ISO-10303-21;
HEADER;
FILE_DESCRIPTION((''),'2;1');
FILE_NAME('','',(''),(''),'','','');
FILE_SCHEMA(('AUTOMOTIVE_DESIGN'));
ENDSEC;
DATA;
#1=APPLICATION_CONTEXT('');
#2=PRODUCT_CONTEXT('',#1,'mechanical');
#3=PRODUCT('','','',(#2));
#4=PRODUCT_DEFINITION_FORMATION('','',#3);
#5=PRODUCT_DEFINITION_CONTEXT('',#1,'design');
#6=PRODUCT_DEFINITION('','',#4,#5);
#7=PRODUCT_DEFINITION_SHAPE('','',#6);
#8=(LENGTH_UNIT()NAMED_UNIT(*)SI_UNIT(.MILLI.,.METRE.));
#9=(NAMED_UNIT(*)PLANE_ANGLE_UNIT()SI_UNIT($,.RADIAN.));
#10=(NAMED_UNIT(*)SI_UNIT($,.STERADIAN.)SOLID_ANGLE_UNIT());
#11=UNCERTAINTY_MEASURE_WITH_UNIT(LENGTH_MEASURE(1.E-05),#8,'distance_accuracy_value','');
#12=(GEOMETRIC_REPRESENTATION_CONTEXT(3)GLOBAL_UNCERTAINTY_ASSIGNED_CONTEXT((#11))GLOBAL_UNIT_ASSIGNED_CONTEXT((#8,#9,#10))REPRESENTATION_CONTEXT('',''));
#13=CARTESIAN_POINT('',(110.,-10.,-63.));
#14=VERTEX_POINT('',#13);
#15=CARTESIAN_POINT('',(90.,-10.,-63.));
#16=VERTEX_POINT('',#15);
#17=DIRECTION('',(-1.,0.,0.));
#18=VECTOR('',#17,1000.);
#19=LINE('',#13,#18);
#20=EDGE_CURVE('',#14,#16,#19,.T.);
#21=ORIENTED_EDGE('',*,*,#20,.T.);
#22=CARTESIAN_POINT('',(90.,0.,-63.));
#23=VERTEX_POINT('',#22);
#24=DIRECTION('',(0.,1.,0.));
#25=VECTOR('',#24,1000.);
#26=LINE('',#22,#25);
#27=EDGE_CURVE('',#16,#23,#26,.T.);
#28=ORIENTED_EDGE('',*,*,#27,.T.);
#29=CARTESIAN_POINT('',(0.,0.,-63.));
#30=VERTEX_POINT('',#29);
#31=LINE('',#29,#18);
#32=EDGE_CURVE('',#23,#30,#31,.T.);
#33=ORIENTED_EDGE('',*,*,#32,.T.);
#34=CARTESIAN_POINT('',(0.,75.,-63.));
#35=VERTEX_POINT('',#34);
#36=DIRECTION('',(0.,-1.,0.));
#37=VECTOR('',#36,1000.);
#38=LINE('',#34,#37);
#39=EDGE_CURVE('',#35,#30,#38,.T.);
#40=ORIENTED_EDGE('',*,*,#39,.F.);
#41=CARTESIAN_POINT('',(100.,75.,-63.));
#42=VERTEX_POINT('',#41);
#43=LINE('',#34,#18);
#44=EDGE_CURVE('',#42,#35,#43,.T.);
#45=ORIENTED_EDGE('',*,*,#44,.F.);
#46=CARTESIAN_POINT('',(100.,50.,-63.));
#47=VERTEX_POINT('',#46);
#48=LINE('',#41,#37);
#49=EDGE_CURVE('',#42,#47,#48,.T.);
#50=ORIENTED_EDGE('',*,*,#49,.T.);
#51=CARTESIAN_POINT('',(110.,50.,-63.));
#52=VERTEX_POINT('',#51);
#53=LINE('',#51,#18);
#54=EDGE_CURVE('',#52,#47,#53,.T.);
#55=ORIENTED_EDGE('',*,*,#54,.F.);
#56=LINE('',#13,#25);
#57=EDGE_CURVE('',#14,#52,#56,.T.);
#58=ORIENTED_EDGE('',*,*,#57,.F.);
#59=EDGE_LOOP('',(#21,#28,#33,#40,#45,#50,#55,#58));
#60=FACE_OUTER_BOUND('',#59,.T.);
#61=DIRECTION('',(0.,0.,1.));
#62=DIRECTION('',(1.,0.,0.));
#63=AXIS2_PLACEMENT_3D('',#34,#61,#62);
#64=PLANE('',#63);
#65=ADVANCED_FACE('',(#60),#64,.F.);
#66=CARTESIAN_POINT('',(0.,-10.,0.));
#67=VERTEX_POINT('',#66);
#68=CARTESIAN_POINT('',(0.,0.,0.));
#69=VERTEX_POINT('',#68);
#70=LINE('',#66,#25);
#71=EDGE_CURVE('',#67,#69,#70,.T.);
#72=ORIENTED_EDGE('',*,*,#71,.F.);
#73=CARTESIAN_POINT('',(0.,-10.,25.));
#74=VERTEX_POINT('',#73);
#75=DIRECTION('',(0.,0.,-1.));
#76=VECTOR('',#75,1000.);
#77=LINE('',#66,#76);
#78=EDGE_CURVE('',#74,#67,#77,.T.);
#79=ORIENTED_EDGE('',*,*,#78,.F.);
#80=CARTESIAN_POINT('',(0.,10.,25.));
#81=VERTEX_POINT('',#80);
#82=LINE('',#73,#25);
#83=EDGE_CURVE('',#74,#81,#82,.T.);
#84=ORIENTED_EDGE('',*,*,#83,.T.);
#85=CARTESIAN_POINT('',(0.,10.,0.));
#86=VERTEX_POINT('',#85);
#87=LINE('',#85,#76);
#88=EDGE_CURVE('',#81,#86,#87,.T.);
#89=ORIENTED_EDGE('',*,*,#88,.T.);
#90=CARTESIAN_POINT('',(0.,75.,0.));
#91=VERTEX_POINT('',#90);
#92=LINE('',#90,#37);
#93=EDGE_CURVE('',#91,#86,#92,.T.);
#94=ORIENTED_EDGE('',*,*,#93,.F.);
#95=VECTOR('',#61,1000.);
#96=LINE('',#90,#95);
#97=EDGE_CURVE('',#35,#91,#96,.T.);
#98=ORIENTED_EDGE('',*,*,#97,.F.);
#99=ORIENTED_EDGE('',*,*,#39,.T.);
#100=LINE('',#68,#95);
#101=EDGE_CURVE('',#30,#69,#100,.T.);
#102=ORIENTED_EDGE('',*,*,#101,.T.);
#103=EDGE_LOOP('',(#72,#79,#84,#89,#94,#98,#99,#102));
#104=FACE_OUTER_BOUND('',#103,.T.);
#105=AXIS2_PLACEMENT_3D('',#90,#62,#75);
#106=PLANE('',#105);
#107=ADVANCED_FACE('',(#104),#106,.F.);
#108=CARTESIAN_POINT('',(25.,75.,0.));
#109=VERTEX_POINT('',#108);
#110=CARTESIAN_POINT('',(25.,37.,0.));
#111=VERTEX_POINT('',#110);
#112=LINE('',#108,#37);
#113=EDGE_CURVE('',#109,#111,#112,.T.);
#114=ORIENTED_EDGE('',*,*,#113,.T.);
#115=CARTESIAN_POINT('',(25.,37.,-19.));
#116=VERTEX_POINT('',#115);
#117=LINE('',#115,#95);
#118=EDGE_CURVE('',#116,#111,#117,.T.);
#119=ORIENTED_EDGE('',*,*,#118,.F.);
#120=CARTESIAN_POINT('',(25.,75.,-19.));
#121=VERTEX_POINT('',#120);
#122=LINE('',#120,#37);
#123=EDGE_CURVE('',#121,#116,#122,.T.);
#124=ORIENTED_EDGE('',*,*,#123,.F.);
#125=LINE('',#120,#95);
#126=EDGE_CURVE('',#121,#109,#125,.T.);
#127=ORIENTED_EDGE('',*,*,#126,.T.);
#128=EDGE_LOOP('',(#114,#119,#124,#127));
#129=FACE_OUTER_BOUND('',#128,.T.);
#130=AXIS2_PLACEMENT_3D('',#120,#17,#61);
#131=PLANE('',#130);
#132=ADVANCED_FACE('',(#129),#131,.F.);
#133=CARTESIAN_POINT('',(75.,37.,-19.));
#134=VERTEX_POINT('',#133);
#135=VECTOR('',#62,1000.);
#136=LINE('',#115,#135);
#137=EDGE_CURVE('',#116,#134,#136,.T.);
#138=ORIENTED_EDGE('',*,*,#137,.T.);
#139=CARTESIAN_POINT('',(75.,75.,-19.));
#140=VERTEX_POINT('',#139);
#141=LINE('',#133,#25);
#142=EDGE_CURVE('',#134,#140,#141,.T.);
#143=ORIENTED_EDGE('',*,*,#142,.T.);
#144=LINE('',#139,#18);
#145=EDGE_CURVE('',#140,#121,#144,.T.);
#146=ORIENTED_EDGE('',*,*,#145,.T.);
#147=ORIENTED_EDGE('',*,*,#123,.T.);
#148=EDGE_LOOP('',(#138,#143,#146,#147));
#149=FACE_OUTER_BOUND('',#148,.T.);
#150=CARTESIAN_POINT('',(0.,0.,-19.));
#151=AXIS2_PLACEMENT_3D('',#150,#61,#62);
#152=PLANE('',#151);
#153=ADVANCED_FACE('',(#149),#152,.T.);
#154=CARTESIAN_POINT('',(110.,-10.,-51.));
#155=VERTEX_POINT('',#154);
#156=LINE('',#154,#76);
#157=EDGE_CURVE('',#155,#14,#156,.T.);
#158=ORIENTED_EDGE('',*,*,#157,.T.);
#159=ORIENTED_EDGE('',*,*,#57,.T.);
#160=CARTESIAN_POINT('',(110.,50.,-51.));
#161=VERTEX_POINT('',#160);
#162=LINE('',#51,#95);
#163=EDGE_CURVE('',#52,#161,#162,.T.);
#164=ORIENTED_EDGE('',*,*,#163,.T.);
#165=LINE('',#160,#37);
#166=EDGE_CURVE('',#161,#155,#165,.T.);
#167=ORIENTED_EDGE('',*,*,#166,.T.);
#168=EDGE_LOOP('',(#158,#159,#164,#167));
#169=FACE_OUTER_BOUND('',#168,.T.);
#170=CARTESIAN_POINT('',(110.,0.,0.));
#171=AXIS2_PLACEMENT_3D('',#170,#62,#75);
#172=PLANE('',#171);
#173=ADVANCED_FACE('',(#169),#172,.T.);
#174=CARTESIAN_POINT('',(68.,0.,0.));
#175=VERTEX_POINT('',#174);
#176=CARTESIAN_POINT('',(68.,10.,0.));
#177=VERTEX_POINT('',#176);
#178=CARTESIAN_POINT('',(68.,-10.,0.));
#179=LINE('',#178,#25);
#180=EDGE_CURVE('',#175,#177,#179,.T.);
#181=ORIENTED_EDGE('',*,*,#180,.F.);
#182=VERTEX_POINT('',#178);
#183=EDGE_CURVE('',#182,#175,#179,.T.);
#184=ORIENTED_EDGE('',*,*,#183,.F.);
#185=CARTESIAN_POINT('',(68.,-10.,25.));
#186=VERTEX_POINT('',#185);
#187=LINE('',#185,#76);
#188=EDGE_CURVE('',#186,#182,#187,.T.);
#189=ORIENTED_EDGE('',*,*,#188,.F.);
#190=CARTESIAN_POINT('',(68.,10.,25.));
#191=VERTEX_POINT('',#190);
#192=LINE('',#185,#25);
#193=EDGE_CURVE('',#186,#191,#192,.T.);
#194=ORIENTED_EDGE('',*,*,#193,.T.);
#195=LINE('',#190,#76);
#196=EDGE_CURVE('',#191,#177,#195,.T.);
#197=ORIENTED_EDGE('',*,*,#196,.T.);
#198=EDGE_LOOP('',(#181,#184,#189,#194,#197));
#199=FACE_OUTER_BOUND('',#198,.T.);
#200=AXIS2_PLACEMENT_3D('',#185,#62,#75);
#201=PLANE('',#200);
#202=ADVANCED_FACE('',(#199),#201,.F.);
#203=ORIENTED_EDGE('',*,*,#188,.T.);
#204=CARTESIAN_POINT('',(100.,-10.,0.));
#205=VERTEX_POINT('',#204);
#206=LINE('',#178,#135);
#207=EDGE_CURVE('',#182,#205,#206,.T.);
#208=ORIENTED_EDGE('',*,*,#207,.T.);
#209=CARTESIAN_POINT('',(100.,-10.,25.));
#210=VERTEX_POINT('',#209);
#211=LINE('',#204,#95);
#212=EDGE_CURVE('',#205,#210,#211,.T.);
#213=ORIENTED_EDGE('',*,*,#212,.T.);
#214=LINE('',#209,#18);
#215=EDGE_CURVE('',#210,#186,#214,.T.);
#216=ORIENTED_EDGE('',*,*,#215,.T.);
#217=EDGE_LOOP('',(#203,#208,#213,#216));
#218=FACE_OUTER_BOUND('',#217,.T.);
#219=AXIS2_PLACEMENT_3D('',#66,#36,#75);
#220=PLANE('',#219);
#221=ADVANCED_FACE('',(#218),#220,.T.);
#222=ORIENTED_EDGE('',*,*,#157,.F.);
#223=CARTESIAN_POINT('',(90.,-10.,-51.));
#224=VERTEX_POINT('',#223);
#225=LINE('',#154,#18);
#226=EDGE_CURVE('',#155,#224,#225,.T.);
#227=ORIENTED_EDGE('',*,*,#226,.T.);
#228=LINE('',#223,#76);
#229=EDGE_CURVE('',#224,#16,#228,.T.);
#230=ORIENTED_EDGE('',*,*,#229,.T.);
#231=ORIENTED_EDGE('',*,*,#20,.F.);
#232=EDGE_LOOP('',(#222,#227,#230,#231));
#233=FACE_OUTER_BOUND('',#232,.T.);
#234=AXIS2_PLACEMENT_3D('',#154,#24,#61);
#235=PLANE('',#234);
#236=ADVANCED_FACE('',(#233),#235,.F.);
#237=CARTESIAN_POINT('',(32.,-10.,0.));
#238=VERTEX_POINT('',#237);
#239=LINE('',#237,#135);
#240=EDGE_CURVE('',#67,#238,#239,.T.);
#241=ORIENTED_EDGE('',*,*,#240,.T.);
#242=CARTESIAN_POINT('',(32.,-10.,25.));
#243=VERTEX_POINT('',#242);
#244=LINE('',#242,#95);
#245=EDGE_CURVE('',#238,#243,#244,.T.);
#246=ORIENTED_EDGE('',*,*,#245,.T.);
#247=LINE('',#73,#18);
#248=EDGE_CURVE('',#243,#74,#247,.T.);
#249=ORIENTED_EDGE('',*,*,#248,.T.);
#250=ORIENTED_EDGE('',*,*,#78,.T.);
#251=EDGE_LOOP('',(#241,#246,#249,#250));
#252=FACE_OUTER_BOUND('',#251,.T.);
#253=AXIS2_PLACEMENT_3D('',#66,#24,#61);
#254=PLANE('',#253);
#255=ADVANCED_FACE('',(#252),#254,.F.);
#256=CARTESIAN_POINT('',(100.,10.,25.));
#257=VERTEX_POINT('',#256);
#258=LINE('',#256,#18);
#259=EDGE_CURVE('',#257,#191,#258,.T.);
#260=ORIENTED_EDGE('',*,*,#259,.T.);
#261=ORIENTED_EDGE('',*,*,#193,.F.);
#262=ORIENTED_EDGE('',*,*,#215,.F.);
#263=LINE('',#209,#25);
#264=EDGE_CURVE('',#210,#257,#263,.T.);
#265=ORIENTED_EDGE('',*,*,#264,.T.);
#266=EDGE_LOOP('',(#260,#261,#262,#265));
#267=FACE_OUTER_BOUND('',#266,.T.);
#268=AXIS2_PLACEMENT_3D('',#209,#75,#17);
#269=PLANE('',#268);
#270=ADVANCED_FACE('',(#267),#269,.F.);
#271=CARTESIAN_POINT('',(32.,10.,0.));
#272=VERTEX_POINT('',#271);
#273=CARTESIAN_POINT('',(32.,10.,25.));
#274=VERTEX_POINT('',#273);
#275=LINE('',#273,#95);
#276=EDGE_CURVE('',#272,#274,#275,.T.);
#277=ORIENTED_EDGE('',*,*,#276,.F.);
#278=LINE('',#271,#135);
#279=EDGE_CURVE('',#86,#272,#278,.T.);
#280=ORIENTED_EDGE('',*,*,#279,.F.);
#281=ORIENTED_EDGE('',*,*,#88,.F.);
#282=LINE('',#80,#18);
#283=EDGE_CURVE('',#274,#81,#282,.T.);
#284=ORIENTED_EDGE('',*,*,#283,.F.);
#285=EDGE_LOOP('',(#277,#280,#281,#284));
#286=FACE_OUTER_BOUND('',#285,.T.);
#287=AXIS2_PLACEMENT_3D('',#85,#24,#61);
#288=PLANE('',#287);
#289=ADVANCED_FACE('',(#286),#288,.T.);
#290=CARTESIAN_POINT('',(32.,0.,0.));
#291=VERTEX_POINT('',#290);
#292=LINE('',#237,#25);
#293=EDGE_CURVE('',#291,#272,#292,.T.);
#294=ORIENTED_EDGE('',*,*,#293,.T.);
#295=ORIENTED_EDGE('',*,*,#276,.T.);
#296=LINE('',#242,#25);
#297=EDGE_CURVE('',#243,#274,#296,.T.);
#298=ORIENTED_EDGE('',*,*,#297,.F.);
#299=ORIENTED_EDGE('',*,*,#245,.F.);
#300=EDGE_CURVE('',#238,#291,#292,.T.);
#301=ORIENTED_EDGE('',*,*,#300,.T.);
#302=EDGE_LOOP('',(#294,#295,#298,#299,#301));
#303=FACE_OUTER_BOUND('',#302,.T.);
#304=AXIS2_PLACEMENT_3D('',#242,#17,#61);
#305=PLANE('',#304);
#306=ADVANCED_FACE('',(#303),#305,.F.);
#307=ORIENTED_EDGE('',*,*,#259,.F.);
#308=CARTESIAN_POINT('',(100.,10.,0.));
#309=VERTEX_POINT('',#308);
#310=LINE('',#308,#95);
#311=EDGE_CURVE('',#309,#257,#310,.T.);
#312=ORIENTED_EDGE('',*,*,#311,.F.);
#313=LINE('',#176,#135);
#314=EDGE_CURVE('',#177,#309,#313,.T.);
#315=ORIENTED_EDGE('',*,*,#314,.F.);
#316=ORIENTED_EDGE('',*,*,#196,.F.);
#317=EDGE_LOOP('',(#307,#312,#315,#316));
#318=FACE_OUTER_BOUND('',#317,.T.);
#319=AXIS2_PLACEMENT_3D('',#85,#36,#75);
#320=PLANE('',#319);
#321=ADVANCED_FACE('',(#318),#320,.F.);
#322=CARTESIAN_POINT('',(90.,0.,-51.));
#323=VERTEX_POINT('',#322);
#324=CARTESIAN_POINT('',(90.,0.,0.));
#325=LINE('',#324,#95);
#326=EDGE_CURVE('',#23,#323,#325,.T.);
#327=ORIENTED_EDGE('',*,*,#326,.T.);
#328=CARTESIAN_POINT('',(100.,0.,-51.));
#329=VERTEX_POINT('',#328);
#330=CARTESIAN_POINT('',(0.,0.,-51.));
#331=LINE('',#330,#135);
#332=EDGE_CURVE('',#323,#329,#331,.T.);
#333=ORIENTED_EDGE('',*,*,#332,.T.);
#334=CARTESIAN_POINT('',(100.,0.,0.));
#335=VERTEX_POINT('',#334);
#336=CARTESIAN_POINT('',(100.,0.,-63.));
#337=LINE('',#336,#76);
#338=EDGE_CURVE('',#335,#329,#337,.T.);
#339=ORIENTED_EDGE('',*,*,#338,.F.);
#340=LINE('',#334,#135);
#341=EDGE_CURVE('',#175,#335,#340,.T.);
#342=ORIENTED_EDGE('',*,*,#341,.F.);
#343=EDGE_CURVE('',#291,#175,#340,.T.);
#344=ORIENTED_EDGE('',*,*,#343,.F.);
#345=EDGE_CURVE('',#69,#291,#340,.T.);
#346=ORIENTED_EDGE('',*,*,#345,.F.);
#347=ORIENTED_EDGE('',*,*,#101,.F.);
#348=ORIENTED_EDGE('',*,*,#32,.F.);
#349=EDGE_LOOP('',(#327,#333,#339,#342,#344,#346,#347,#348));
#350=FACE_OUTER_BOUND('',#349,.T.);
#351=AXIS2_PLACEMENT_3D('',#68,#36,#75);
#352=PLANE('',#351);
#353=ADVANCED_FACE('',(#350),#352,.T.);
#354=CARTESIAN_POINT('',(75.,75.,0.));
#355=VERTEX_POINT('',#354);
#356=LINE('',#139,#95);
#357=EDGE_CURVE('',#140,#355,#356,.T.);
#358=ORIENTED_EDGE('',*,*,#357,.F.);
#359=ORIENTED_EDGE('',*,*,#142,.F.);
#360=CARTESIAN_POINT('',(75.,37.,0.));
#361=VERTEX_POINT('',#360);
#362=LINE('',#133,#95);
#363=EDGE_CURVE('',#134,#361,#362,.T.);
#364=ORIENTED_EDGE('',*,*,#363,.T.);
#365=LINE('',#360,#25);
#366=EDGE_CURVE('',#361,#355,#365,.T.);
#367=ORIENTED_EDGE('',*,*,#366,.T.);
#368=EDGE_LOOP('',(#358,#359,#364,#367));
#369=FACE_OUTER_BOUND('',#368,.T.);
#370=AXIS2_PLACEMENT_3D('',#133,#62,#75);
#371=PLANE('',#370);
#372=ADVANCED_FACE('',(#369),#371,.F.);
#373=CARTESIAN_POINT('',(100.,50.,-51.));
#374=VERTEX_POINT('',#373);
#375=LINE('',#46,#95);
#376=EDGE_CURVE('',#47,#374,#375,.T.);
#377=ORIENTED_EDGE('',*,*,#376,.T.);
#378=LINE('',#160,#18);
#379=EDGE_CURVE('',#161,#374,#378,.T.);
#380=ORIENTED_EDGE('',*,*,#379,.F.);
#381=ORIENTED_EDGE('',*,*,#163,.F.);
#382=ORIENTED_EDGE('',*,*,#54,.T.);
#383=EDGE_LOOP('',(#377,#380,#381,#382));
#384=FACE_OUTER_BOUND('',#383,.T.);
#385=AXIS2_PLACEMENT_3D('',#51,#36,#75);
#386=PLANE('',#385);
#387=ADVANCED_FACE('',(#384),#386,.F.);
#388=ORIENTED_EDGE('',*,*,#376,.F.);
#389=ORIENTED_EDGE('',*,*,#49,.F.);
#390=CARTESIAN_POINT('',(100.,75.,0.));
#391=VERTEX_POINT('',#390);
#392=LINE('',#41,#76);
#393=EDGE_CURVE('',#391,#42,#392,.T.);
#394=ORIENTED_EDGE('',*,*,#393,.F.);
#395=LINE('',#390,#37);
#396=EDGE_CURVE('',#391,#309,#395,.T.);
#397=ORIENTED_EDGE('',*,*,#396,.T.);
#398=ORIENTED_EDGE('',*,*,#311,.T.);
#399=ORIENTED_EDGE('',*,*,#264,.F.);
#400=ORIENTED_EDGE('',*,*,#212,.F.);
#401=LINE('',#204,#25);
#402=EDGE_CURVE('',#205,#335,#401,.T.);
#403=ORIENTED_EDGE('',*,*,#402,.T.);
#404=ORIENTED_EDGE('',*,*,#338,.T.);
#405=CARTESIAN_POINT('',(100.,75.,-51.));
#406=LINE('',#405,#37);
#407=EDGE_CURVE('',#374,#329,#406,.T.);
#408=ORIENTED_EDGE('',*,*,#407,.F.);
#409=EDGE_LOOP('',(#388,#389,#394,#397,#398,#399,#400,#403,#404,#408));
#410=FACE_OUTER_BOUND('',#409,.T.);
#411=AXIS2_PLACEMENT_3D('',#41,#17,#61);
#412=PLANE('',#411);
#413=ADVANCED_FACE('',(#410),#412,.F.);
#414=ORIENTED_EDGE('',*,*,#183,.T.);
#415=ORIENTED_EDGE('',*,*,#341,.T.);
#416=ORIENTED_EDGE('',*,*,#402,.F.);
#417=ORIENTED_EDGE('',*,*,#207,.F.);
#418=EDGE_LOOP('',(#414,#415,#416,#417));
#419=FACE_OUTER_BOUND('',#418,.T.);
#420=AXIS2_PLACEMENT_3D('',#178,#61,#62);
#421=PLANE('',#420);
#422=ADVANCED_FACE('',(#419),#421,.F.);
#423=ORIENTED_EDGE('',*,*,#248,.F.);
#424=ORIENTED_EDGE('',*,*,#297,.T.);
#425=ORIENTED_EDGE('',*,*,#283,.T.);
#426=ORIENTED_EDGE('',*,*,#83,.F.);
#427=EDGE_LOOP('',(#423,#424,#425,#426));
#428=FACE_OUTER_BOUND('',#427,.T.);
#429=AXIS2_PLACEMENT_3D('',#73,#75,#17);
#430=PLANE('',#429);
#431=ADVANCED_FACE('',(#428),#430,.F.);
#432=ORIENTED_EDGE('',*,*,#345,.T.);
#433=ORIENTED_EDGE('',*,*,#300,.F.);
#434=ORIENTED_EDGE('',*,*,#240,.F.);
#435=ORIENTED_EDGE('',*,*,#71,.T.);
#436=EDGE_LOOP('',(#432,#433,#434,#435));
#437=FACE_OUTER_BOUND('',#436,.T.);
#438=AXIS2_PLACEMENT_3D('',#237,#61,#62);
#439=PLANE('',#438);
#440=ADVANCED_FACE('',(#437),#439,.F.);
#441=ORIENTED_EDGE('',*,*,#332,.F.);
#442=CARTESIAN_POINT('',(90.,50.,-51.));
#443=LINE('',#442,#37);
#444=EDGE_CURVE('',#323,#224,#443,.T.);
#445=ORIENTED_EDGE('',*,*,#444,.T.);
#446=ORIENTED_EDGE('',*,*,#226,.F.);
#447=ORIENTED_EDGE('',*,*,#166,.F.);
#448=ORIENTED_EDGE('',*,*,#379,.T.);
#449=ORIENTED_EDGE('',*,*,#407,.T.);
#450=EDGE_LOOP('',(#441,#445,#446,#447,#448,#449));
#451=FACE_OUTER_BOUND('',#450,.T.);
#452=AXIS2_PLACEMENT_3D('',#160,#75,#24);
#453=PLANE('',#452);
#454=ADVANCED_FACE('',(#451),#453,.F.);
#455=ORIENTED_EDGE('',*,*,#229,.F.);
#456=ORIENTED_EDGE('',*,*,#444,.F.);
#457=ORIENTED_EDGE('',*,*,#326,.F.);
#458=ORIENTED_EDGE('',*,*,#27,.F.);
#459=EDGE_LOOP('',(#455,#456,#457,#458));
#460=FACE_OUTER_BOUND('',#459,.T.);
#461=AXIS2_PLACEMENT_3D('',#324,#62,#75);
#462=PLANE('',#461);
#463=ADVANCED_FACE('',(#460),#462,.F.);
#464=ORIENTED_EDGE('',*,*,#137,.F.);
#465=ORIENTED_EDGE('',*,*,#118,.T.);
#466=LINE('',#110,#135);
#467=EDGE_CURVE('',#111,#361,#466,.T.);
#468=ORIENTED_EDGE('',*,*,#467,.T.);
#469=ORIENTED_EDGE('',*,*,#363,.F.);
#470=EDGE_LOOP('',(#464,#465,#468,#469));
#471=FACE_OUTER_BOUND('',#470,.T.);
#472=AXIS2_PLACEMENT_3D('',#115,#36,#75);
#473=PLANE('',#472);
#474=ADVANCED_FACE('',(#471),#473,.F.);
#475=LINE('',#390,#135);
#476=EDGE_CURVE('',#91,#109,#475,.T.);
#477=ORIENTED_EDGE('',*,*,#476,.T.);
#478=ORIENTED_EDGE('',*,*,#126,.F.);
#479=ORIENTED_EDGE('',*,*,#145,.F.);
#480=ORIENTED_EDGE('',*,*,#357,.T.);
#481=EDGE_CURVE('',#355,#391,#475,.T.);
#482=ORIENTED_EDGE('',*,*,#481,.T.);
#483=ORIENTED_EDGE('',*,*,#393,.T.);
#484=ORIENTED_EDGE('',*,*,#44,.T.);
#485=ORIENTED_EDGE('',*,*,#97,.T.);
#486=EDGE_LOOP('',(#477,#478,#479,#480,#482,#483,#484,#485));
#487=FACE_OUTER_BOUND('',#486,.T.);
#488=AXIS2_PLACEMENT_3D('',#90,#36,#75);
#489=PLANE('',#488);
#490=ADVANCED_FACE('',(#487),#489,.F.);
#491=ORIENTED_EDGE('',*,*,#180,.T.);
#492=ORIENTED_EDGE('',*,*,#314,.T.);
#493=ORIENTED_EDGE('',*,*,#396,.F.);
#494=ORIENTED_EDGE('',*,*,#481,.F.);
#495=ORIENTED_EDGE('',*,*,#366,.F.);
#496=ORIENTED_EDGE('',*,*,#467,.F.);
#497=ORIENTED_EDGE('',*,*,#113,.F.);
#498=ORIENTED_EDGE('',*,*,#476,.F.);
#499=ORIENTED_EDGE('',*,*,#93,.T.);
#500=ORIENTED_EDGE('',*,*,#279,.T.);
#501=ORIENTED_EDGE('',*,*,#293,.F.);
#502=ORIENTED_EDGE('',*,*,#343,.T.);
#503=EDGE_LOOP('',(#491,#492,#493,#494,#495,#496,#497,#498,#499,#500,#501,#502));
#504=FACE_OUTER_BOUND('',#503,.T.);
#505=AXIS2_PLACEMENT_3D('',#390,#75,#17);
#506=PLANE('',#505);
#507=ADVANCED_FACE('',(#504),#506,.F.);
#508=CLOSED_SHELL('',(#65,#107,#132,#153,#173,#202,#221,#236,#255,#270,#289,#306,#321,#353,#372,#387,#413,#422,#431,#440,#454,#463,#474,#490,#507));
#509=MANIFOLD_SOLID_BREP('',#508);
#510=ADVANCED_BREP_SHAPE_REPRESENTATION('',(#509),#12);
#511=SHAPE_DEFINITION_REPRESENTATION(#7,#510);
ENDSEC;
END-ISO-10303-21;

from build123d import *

# Parameters (mm, degrees)
BASE_BLOCK_SKETCH_W        = 100
BASE_BLOCK_SKETCH_H        = 63
BASE_BLOCK_100X63X75_DEPTH = 75
TOP_POCKET_SKETCH_W        = 50
TOP_POCKET_SKETCH_H        = 38
TOP_POCKET_38X25X19_DEPTH  = 19
FEET_SKETCH_W              = 32
FEET_SKETCH_H              = 25
FEET_2X_32X25_DEPTH        = 10
SIDE_RIB_DEPTH             = 10


with BuildPart() as part:
    # Base Block Sketch → Base Block 100x63x75 (new body)
    with BuildSketch(Plane(origin=(0, 0, 0), x_dir=(1, 0, 0), z_dir=(0, 1, 0))):
        with Locations((50, 31.5)):
            Rectangle(BASE_BLOCK_SKETCH_W, BASE_BLOCK_SKETCH_H)
    extrude(amount=BASE_BLOCK_100X63X75_DEPTH)

    # Top Pocket Sketch → Top Pocket 38x25x19 (cut)
    with BuildSketch(Plane.XY):
        with Locations((50, 56)):
            Rectangle(TOP_POCKET_SKETCH_W, TOP_POCKET_SKETCH_H)
    extrude(amount=-TOP_POCKET_38X25X19_DEPTH, mode=Mode.SUBTRACT)

    # Feet Sketch → Feet 2x 32x25 (add, symmetric)
    with BuildSketch(Plane.XZ):
        with Locations((16, 12.5)):
            Rectangle(FEET_SKETCH_W, FEET_SKETCH_H)
        with Locations((84, 12.5)):
            Rectangle(FEET_SKETCH_W, FEET_SKETCH_H)
    extrude(amount=FEET_2X_32X25_DEPTH, both=True)

    # Side Rib Sketch → Side Rib (add, symmetric)
    with BuildSketch(Plane(origin=(100, 0, 0), x_dir=(0, 0, -1), z_dir=(1, 0, 0))):
        Polygon((63, 0), (63, 50), (51, 50), (51, -10), (63, -10), align=None)
    extrude(amount=SIDE_RIB_DEPTH, both=True)


solid = part.part
